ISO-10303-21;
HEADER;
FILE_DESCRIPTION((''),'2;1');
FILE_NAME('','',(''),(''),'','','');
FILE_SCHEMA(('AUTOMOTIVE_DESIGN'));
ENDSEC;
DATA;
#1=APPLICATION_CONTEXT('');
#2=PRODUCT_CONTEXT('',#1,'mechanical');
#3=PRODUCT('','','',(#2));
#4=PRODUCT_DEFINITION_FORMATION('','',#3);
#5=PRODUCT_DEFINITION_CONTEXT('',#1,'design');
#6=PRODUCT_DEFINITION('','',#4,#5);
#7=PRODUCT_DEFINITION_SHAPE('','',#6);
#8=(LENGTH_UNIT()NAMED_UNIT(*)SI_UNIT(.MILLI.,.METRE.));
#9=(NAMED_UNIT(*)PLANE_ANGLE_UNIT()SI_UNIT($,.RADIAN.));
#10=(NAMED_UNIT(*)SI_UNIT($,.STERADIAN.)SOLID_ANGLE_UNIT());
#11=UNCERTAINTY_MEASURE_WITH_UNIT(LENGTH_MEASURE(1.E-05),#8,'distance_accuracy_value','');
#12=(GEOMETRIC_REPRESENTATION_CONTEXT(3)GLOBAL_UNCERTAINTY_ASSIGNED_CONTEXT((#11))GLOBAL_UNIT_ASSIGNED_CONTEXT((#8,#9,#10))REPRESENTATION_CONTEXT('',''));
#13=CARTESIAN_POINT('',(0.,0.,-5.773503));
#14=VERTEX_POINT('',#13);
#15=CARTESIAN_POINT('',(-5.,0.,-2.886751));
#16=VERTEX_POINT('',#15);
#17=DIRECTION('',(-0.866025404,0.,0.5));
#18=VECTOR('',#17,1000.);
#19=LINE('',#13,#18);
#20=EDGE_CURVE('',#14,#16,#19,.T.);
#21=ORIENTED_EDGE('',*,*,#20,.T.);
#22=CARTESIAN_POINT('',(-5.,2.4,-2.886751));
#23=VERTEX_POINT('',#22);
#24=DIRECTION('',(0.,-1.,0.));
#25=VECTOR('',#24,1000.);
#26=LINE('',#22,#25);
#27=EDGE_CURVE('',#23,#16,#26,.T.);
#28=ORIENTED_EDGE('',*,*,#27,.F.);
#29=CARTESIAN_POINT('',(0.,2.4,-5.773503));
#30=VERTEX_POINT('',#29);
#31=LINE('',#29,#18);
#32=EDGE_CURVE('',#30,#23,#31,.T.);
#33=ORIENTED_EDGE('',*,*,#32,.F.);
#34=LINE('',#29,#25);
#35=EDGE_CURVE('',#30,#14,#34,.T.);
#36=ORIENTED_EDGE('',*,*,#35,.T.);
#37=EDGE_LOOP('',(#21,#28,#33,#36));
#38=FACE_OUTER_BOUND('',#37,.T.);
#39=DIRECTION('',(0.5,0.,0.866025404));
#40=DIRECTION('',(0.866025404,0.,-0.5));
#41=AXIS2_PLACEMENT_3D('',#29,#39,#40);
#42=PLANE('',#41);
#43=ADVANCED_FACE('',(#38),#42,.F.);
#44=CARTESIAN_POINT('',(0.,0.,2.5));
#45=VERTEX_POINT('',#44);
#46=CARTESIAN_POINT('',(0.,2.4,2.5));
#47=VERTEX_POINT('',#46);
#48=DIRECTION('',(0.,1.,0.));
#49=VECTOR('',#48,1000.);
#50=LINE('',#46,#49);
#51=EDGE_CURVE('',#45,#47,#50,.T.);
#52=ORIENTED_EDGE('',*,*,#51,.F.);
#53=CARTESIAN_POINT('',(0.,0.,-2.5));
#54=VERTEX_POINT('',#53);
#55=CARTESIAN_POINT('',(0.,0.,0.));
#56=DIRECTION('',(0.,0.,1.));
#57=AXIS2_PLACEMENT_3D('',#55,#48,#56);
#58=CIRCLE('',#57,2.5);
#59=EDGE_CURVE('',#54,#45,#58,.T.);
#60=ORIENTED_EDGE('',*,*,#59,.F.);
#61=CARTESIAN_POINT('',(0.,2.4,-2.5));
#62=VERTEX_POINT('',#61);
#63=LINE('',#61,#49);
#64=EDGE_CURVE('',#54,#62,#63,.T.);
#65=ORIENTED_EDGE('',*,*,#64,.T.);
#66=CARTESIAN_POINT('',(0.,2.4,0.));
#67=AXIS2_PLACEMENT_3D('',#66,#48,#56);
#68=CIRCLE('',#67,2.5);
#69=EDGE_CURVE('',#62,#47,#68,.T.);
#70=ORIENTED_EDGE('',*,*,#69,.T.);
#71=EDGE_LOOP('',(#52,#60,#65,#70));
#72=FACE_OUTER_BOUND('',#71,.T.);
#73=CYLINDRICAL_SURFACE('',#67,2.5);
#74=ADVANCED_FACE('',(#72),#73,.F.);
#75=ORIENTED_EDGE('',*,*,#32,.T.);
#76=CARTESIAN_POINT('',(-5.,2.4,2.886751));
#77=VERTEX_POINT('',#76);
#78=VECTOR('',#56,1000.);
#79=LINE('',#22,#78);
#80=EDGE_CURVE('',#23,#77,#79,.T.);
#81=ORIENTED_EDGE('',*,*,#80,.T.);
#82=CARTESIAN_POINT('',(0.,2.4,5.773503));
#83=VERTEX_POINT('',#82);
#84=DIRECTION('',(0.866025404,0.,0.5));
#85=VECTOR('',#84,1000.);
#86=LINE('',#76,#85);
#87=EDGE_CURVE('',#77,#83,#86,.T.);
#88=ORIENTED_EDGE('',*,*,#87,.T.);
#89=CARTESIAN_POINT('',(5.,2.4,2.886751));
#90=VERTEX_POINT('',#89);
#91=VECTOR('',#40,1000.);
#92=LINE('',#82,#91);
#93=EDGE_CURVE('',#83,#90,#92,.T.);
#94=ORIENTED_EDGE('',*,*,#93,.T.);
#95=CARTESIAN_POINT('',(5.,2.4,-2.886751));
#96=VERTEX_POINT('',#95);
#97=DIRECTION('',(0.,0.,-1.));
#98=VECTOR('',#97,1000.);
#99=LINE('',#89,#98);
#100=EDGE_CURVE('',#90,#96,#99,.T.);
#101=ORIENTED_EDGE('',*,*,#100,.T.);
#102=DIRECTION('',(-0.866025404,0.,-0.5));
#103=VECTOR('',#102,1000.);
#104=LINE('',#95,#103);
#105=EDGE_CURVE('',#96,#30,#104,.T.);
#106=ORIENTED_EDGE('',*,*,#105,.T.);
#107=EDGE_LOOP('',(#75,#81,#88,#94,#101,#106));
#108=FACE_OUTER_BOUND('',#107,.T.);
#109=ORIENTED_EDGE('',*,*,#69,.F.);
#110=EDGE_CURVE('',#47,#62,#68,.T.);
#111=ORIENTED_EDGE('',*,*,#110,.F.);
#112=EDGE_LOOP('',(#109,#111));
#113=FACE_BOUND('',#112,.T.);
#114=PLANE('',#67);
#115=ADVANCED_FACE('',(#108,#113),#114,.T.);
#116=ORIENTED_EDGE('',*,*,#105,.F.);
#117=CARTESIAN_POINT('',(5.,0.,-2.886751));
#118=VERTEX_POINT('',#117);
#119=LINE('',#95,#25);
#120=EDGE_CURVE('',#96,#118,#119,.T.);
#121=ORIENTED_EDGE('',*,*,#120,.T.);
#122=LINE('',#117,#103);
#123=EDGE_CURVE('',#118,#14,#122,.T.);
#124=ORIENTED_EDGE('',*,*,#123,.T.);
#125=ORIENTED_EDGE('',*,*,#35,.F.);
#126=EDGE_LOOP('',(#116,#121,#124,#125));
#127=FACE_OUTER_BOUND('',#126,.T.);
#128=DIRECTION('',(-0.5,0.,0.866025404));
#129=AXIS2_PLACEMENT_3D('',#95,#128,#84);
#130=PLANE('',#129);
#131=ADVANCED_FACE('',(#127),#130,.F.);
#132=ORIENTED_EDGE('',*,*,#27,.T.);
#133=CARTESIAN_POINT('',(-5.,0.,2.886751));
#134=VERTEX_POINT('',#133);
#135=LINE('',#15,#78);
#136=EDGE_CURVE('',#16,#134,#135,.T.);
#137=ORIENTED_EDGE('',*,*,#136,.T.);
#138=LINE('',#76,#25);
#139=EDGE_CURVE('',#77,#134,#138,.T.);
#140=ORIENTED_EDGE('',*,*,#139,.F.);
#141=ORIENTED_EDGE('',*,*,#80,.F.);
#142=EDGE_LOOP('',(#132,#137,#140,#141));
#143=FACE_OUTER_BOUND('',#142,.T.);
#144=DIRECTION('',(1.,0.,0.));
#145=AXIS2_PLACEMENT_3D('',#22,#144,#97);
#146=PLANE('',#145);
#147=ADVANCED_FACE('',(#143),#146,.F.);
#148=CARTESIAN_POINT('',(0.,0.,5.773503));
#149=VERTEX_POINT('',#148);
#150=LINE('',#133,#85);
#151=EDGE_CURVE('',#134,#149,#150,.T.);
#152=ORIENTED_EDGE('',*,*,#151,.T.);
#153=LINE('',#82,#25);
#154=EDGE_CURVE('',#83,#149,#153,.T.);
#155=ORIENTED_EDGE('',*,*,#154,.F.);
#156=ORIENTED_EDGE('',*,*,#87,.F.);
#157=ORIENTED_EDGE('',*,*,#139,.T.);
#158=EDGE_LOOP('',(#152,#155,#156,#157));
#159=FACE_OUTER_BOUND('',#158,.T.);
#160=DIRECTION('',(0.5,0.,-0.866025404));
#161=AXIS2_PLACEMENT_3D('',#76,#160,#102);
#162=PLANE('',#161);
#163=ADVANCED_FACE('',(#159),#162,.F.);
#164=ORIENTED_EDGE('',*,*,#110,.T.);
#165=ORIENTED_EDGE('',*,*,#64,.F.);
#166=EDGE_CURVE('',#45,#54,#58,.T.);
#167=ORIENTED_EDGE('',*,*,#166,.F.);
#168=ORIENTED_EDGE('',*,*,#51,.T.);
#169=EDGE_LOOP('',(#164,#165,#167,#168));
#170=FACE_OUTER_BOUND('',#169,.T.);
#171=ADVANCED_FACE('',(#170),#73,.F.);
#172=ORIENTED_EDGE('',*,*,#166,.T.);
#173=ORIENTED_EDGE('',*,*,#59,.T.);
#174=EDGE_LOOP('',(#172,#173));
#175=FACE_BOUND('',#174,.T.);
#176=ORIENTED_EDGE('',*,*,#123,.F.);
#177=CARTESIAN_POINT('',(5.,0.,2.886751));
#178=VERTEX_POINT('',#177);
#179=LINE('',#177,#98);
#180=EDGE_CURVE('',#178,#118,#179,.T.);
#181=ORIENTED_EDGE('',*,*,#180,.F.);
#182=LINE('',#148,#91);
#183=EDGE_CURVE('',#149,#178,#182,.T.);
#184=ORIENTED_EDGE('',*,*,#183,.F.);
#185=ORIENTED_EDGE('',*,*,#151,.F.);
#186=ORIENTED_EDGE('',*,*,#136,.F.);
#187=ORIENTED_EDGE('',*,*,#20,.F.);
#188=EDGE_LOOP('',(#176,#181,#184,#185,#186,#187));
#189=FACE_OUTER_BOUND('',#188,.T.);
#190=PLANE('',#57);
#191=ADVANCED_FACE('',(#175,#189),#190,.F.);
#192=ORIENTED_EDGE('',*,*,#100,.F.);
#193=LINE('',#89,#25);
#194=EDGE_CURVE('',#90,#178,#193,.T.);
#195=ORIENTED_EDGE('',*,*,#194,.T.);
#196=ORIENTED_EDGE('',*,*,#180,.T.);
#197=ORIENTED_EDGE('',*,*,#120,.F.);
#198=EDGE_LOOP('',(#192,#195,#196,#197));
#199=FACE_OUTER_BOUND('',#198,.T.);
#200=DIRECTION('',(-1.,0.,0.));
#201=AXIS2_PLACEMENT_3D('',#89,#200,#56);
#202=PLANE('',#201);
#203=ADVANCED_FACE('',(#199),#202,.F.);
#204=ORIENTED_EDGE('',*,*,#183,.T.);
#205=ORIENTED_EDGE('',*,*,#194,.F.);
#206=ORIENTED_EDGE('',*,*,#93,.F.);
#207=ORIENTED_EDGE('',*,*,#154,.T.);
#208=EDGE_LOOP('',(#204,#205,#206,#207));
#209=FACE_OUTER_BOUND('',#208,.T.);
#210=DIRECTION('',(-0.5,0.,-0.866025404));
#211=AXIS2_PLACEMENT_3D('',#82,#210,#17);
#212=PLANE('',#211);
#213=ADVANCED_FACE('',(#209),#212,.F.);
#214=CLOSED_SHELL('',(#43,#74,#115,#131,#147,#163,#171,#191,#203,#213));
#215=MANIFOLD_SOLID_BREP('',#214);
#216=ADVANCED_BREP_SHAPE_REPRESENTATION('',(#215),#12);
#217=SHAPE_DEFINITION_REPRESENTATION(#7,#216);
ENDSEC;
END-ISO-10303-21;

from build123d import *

# Parameters (mm, degrees)
EXTRUDE_1_DEPTH    = 2.4
HOLE_WIZARD_M6_1_D = 5


with BuildPart() as part:
    # 草图1 → 凸台-拉伸1 (new body)
    with BuildSketch(Plane(origin=(0, 0, 0), x_dir=(1, 0, 0), z_dir=(0, 1, 0))):
        Polygon((0, 5.773502692), (-5, 2.886751346), (-5, -2.886751346), (0, -5.773502692), (5, -2.886751346), (5, 2.886751346), align=None)
    extrude(amount=EXTRUDE_1_DEPTH)

    # M6 螺纹孔1 (through all)
    with Locations(Plane(origin=(0, 2.4, 0), x_dir=(1, 0, 0), z_dir=(0, 1, 0))):
        with Locations((0, 0)):
            Hole(HOLE_WIZARD_M6_1_D / 2)


solid = part.part
